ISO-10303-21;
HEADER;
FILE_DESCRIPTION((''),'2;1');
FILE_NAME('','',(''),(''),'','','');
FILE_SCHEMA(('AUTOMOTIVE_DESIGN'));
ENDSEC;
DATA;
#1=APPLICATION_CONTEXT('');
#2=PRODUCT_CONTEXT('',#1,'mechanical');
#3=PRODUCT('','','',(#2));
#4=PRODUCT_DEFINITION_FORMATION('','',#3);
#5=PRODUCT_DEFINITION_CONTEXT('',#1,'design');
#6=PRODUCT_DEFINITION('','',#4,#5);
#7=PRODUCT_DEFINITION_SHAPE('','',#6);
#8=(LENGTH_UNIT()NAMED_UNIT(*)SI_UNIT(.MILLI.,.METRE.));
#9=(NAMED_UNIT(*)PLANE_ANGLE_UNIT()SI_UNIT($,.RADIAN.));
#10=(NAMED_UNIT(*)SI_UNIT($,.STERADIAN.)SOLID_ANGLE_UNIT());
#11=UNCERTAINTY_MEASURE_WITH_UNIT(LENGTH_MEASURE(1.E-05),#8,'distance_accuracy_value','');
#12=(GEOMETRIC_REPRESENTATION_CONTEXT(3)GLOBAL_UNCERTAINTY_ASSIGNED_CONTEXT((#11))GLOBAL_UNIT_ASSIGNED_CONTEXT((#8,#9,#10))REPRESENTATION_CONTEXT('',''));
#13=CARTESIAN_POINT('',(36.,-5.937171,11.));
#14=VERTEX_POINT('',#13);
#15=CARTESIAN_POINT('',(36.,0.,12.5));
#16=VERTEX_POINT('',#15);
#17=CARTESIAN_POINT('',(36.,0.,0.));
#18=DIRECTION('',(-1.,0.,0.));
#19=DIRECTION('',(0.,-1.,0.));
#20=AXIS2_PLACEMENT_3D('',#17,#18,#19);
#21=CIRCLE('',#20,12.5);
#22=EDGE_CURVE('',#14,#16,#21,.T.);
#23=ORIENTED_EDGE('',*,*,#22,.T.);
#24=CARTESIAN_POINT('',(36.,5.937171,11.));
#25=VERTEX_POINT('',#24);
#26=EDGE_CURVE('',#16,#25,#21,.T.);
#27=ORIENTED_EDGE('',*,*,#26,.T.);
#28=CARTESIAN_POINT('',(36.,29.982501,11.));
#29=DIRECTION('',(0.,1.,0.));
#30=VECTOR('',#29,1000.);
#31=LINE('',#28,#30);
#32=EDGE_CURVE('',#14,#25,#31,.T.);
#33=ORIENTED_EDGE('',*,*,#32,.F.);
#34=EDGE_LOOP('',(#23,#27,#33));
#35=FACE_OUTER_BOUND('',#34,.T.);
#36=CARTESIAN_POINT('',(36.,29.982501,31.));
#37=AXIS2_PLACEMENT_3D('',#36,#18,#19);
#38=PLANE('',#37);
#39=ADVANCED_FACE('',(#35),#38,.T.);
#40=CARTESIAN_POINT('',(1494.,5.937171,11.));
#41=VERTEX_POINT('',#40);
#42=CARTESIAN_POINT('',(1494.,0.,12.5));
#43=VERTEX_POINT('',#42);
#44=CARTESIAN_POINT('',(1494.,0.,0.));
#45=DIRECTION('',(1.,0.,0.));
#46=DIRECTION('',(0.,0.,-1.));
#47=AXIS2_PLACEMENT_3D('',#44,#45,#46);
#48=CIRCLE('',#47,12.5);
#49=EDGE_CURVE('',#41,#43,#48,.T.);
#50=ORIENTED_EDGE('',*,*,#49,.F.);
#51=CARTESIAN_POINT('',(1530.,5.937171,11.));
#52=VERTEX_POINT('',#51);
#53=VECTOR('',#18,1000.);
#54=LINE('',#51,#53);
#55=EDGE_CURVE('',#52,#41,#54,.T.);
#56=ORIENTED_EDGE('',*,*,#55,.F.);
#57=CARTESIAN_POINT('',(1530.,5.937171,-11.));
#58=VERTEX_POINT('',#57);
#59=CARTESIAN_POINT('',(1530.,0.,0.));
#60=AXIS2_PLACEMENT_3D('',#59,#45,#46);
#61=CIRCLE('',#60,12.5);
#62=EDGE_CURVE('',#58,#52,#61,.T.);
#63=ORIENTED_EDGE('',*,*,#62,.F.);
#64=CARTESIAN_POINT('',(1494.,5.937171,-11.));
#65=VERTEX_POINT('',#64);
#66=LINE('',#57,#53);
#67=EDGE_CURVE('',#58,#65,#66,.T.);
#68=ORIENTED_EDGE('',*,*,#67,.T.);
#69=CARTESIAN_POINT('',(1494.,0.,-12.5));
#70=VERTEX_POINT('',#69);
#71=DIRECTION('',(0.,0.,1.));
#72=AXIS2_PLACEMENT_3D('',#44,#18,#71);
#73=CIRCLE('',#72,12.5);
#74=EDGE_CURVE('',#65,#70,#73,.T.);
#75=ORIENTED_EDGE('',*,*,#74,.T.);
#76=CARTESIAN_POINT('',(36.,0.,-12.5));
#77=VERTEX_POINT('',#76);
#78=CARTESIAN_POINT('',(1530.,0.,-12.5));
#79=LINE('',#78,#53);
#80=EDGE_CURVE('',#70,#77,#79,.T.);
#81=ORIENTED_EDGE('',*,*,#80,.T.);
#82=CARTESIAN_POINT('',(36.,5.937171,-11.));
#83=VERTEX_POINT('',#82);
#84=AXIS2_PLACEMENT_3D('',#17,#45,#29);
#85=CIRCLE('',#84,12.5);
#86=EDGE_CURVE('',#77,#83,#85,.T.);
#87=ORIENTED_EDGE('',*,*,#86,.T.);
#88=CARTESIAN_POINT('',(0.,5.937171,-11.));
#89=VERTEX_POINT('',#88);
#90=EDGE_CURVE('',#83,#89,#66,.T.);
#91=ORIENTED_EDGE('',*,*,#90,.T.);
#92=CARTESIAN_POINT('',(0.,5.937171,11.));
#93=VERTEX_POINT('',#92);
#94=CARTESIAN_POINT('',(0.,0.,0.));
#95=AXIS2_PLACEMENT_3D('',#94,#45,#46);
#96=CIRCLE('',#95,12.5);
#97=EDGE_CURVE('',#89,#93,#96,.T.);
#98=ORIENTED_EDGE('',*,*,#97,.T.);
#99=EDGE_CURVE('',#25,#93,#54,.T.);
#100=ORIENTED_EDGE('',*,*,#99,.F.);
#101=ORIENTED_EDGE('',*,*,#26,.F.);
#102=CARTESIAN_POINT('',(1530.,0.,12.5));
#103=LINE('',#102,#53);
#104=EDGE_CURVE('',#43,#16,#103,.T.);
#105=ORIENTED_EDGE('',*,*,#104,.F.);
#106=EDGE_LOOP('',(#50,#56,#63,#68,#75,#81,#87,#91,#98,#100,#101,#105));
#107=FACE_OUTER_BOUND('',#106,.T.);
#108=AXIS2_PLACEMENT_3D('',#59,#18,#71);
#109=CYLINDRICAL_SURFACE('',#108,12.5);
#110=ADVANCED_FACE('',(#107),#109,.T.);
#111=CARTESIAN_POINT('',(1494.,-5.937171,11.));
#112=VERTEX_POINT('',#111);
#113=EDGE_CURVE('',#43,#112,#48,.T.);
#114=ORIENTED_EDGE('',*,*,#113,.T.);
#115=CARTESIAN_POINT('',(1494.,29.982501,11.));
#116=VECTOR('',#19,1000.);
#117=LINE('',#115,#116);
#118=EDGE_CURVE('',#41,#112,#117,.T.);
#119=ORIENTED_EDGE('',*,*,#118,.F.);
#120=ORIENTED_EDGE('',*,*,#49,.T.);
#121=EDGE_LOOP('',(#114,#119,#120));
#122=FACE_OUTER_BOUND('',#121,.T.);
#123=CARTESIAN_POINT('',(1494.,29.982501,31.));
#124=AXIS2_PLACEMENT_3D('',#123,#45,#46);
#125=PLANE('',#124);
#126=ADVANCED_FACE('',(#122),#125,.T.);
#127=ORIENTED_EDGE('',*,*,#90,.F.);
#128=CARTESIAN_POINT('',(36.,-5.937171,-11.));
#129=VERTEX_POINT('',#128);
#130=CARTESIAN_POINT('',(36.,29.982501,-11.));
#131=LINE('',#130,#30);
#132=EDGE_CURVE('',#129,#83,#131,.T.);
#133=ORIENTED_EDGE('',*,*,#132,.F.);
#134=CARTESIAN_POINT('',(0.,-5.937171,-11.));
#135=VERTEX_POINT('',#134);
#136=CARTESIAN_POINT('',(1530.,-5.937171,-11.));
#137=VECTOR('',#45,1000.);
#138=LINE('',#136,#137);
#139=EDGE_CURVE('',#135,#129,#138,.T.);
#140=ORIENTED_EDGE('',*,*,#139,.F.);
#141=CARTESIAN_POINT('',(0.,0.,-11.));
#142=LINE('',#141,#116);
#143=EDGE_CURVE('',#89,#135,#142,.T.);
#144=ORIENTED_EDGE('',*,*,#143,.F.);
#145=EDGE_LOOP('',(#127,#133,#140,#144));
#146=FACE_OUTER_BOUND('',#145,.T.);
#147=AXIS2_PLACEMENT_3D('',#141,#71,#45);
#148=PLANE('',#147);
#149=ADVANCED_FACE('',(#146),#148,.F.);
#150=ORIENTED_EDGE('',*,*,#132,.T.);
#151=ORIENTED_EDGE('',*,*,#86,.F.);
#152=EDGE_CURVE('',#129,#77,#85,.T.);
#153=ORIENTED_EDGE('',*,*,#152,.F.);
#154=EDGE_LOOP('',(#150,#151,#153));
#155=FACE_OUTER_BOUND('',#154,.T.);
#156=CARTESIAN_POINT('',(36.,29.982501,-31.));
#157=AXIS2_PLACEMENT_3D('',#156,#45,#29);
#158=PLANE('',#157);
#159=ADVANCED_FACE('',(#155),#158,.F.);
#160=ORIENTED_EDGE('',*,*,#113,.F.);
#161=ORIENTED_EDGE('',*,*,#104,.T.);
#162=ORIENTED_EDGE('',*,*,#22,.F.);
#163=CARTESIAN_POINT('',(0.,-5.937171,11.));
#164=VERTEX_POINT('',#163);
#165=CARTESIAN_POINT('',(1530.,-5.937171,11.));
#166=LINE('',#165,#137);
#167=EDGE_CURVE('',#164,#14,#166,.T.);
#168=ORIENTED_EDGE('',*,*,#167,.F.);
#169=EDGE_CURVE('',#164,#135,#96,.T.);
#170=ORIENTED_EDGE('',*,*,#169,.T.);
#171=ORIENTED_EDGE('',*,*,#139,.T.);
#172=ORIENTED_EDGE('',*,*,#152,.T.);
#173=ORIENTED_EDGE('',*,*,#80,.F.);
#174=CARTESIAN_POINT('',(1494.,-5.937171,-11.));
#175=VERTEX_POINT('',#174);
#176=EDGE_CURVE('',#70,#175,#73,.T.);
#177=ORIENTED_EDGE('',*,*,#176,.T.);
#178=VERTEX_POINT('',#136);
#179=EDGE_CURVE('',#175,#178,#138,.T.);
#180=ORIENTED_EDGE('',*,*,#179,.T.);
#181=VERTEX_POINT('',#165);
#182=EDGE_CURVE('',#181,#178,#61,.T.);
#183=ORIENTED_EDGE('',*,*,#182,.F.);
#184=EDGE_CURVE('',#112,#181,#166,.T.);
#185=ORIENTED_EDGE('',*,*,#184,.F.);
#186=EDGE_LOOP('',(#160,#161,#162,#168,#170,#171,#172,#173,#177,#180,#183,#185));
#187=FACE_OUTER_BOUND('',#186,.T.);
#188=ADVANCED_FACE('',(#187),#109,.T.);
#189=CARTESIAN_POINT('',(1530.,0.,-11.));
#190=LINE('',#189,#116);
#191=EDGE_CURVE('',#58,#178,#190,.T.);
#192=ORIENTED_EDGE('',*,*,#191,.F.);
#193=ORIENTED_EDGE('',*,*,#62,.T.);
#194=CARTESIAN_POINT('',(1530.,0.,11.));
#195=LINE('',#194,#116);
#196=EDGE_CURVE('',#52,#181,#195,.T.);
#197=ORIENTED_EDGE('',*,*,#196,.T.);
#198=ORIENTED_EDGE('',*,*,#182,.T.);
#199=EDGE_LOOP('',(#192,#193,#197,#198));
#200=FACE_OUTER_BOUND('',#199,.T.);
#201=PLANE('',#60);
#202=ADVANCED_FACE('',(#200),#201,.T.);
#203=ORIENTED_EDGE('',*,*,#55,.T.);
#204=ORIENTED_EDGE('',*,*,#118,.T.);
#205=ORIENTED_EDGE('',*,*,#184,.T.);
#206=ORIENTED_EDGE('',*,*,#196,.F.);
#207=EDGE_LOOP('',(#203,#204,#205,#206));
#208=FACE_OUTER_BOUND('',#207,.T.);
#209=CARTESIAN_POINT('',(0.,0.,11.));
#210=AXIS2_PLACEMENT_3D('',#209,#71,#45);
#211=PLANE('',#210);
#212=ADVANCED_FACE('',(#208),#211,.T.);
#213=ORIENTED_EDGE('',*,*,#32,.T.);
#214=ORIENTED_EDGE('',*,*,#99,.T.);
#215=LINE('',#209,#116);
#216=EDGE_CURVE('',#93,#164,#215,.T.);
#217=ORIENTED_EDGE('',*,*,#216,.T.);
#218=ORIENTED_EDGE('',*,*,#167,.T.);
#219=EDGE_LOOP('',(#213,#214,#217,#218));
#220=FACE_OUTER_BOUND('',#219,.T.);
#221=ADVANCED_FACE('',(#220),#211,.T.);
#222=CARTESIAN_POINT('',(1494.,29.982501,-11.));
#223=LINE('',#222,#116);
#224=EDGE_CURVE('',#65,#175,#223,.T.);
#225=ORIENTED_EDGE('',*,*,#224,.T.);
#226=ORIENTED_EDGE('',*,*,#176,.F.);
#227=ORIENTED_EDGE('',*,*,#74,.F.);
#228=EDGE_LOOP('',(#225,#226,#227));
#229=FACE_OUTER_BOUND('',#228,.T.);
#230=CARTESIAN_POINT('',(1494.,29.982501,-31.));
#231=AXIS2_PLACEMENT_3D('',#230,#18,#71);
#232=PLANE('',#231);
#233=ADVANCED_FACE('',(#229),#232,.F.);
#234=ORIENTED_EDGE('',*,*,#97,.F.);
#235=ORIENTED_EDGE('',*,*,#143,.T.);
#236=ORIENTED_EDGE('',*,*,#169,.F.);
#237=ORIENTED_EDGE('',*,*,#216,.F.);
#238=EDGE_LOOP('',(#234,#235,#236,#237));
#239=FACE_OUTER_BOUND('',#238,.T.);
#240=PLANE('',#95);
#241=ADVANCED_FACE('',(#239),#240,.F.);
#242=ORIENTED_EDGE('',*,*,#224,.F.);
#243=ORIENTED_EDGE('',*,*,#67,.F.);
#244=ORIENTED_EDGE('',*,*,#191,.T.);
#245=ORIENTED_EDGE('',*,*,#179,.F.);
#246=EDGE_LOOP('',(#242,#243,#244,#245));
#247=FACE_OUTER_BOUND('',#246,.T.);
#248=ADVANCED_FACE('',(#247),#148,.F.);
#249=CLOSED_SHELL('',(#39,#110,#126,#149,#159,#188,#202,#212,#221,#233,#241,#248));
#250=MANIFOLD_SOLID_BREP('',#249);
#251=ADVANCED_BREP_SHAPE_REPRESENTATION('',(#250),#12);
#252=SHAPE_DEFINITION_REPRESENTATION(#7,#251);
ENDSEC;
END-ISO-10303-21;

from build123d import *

# Parameters (mm, degrees)
SKETCH1_R           = 12.5
BOSS_EXTRUDE1_DEPTH = 1530
CUT_EXTRUDE1_START  = -11
SKETCH_2_2_W        = 44.374102045
SKETCH_2_2_H        = 48.77153558
SKETCH_2_2_W_2      = 134.556182266
SKETCH_2_2_H_2      = 57.966169337
CUT_EXTRUDE1_DEPTH  = 20
CUT_EXTRUDE2_START  = 11
SKETCH_2_2_2_W      = 44.374102045
SKETCH_2_2_2_H      = 48.77153558
SKETCH_2_2_2_W_2    = 134.556182266
SKETCH_2_2_2_H_2    = 57.966169337
CUT_EXTRUDE2_DEPTH  = 20


with BuildPart() as part:
    # Sketch1 → Boss-Extrude1 (new body)
    with BuildSketch(Plane(origin=(0, 0, 0), x_dir=(0, 0, -1), z_dir=(1, 0, 0))):
        Circle(SKETCH1_R)
    extrude(amount=BOSS_EXTRUDE1_DEPTH)

    # Sketch 2_2 → Cut-Extrude1 (cut)
    with BuildSketch(Plane.XY.offset(CUT_EXTRUDE1_START)):
        with Locations((13.812948977, 5.596733591)):
            Rectangle(SKETCH_2_2_W, SKETCH_2_2_H)
        with Locations((1561.278091133, 0.999416713)):
            Rectangle(SKETCH_2_2_W_2, SKETCH_2_2_H_2)
    extrude(amount=-CUT_EXTRUDE1_DEPTH, mode=Mode.SUBTRACT)

    # Sketch 2_2 2 → Cut-Extrude2 (cut)
    with BuildSketch(Plane.XY.offset(CUT_EXTRUDE2_START)):
        with Locations((13.812948977, 5.596733591)):
            Rectangle(SKETCH_2_2_2_W, SKETCH_2_2_2_H)
        with Locations((1561.278091133, 0.999416713)):
            Rectangle(SKETCH_2_2_2_W_2, SKETCH_2_2_2_H_2)
    extrude(amount=CUT_EXTRUDE2_DEPTH, mode=Mode.SUBTRACT)


solid = part.part
